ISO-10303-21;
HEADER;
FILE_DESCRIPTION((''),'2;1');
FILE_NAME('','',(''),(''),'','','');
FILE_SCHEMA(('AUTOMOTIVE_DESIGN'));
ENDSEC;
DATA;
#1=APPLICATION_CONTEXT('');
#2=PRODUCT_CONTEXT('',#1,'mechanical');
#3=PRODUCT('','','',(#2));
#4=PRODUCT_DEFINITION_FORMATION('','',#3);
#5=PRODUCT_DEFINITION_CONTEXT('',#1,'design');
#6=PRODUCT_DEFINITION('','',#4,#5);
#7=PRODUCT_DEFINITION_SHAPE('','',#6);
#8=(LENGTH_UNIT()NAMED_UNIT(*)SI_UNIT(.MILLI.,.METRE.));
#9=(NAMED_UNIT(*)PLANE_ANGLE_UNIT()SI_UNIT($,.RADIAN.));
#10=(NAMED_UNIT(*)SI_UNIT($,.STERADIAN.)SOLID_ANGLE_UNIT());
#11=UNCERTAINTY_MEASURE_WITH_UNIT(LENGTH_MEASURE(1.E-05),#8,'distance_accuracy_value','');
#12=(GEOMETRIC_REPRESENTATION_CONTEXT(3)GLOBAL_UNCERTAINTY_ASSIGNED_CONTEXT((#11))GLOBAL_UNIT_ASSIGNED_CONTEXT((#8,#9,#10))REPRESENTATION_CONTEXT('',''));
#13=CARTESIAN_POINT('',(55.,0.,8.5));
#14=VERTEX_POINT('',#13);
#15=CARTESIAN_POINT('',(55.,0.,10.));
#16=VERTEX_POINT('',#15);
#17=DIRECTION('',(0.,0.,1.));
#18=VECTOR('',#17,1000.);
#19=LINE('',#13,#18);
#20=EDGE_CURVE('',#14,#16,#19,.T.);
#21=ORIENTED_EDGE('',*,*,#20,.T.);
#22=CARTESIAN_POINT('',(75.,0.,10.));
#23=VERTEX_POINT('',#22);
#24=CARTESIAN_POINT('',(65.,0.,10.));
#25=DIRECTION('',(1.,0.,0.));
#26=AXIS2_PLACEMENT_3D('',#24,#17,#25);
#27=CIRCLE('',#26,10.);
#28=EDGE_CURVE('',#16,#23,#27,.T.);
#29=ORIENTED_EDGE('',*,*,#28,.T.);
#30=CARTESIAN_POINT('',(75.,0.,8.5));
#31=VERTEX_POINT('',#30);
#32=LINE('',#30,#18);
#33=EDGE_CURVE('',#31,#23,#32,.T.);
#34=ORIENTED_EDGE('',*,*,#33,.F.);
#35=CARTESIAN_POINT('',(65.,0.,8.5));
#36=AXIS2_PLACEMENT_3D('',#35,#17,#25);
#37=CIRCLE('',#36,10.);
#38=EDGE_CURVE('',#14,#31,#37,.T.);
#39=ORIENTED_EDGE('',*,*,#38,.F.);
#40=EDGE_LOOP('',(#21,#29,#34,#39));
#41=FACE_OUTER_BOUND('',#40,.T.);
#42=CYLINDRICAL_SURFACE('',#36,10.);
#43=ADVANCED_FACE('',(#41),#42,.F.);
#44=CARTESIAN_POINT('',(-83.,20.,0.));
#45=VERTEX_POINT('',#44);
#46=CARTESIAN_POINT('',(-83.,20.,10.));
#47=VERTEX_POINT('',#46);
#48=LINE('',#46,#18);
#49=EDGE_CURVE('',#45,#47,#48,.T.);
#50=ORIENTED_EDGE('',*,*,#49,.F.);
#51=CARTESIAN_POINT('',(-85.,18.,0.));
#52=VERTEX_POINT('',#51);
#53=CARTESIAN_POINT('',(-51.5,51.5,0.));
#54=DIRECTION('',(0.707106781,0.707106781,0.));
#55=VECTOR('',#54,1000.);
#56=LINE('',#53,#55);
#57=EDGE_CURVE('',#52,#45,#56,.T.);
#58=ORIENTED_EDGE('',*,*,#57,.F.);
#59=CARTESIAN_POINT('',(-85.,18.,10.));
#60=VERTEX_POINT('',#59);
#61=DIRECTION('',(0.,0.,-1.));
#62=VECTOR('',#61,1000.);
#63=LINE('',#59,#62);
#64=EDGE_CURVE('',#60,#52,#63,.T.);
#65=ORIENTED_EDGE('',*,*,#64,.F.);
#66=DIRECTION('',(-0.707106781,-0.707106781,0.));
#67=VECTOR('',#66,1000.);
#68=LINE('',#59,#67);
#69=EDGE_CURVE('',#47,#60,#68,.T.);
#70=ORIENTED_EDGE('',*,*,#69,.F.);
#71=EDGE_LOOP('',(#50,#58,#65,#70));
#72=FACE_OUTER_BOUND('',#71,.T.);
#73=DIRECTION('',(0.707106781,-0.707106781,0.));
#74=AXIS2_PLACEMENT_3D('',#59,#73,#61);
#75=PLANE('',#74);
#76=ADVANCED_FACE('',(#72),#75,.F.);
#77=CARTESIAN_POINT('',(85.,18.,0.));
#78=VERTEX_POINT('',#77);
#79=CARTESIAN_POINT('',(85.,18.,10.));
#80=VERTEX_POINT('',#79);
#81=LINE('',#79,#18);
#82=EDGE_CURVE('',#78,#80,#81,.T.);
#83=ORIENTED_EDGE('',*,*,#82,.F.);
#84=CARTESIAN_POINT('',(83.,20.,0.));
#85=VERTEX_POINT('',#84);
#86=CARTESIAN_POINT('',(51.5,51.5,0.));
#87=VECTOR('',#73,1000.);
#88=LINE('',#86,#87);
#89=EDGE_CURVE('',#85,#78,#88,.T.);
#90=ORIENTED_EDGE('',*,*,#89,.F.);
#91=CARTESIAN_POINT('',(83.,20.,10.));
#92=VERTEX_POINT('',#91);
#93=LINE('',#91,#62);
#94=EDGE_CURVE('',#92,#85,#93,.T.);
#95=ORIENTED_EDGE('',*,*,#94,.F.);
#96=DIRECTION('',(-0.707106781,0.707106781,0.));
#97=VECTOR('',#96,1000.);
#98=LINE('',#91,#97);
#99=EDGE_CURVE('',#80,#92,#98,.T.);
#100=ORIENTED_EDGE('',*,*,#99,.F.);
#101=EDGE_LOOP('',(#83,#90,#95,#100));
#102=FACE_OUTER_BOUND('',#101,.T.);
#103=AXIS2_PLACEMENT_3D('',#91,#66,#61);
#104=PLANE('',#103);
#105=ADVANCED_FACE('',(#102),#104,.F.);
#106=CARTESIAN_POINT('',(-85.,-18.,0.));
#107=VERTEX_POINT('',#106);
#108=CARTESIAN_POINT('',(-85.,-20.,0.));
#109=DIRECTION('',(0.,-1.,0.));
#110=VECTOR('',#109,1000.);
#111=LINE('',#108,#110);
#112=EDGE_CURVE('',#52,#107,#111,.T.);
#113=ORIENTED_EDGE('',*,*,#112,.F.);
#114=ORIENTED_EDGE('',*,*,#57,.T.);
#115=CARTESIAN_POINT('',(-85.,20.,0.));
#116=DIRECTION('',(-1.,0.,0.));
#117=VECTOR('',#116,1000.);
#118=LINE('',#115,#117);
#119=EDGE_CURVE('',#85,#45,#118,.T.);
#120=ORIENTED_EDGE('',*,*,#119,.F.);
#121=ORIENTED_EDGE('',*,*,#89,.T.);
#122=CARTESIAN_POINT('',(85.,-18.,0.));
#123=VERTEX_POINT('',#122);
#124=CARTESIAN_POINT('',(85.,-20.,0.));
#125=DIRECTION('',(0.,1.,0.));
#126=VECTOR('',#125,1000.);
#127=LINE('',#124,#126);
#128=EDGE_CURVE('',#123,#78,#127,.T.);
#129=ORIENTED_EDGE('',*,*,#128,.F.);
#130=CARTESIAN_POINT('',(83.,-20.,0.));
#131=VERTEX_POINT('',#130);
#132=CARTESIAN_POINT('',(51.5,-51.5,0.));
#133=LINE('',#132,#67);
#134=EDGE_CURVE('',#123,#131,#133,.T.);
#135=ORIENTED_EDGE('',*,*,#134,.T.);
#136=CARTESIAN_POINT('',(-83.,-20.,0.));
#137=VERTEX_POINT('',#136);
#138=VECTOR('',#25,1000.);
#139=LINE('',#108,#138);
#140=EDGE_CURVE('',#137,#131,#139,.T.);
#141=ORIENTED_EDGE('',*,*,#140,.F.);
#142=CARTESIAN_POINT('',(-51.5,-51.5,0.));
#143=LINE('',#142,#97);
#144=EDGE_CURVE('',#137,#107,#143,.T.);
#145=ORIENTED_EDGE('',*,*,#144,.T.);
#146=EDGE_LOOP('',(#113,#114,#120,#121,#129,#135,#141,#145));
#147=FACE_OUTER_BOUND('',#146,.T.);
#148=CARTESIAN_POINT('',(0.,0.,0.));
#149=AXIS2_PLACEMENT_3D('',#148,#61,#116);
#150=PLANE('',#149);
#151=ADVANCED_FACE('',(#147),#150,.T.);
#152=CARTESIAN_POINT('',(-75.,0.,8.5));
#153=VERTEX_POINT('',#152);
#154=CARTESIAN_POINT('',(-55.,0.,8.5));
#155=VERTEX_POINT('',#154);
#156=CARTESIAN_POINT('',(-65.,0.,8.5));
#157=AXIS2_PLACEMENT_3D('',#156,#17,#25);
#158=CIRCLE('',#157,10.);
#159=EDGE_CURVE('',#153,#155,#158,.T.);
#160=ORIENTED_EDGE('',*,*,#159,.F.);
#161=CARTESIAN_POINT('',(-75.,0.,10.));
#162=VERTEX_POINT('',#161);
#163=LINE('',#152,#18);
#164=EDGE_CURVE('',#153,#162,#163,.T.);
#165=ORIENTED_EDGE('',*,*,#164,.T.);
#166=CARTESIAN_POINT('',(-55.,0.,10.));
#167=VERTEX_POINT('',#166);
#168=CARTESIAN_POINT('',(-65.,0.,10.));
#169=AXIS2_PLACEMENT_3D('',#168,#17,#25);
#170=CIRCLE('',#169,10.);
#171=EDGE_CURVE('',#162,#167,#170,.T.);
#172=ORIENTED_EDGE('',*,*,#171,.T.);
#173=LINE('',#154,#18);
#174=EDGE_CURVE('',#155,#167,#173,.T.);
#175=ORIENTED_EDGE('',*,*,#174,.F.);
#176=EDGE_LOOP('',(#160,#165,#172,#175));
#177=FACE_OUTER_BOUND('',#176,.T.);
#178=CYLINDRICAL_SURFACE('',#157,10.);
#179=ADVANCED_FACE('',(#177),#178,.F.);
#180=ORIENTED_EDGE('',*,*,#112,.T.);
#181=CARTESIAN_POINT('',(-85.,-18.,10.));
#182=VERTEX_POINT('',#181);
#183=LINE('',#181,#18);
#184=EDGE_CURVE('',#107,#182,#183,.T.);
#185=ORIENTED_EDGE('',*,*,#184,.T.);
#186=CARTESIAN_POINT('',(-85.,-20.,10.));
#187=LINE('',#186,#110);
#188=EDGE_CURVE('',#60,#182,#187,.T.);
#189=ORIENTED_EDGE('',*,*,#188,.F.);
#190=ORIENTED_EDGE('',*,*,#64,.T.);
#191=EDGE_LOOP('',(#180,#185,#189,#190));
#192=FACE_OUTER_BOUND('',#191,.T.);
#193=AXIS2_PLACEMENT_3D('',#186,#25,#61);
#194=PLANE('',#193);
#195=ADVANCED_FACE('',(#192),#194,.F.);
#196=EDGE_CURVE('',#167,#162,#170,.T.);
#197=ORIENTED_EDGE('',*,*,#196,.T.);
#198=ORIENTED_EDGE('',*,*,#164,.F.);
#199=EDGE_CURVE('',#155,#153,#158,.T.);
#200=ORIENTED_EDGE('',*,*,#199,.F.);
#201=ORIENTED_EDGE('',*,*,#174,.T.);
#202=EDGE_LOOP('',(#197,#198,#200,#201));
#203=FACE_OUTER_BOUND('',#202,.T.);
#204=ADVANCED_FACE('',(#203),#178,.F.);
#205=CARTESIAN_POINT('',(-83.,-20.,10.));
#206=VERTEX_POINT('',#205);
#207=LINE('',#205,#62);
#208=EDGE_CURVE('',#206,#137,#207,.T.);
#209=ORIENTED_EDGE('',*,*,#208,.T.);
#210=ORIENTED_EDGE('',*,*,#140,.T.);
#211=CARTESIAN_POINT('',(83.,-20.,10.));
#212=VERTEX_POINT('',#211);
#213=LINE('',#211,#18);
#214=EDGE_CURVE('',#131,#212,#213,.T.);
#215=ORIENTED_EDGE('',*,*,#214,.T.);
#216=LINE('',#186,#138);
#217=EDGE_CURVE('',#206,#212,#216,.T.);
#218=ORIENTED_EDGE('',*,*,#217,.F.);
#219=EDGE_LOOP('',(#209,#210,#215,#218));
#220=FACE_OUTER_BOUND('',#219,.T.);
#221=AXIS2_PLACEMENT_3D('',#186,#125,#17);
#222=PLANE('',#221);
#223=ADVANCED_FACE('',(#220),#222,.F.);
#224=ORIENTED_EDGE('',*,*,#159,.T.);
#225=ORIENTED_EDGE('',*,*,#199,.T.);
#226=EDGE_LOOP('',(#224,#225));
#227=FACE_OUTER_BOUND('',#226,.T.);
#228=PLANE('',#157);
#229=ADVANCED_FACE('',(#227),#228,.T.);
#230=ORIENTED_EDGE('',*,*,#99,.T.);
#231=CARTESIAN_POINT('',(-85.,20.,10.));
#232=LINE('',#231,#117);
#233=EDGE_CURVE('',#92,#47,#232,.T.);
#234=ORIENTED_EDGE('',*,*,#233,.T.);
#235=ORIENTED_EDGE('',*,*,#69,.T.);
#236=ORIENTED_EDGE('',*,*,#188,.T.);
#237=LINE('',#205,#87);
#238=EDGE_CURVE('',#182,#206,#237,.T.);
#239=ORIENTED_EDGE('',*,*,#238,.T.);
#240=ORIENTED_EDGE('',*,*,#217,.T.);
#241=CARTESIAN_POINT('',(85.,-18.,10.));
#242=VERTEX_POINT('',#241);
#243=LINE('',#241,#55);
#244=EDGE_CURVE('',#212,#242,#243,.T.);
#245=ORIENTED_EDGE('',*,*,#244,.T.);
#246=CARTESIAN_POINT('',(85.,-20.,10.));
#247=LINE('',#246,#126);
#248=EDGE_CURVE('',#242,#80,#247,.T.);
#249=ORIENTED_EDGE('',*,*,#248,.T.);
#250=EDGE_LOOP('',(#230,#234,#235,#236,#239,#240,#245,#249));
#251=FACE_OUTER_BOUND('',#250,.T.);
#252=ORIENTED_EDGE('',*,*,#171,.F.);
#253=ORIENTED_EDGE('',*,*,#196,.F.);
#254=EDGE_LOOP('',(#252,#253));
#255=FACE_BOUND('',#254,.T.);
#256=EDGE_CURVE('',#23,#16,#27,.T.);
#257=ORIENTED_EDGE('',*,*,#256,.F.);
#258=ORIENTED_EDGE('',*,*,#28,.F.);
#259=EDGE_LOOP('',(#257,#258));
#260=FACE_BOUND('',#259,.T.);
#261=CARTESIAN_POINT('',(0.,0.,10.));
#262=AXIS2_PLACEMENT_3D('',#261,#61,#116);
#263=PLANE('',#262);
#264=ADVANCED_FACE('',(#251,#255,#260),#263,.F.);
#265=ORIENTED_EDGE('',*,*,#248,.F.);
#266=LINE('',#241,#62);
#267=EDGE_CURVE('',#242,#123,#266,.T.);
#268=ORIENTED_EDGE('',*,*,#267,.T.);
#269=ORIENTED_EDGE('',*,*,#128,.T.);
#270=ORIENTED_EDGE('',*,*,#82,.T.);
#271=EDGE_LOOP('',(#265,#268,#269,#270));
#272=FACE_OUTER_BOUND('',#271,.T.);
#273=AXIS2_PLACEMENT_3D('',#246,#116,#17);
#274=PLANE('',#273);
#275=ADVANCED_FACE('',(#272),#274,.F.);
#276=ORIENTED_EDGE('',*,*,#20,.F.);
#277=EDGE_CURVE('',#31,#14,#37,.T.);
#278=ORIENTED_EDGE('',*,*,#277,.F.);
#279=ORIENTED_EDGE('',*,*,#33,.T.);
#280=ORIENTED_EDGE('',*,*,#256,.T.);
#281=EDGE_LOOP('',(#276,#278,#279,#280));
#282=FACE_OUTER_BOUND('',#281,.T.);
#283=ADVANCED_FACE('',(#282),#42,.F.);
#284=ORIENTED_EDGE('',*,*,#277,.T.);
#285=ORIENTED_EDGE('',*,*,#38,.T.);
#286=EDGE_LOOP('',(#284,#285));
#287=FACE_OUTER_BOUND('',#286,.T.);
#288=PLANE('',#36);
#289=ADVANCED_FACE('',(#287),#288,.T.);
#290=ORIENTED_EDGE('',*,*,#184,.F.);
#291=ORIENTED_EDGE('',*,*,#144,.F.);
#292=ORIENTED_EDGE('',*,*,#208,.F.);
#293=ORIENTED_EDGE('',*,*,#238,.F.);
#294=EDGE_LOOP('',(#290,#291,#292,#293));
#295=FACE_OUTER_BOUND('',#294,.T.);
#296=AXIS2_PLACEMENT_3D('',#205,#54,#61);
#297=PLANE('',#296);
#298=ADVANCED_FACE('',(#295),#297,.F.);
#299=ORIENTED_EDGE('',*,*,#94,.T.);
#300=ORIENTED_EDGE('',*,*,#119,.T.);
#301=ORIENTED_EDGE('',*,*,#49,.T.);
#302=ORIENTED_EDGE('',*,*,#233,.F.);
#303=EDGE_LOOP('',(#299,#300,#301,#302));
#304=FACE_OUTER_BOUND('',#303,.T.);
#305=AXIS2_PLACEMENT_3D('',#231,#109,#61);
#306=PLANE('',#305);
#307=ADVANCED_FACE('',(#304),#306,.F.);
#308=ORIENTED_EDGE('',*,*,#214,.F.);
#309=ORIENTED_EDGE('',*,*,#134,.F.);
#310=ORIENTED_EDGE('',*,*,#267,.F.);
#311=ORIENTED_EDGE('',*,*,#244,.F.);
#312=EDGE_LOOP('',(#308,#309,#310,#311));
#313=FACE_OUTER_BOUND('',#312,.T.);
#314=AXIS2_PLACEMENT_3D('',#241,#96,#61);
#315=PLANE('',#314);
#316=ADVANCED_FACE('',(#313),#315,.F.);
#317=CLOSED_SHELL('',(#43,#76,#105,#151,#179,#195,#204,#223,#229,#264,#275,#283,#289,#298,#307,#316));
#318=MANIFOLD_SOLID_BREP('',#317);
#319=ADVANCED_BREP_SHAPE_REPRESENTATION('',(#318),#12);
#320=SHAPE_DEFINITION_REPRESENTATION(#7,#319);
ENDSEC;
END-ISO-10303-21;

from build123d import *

# Parameters (mm, degrees)
SKETCH_1_W          = 170
SKETCH_1_H          = 40
EXTRUDE_1_DEPTH     = 10
SKETCH_2_R          = 10
CUT_EXTRUDE_1_DEPTH = 1.5
CHAMFER_1_SIZE      = 2


with BuildPart() as part:
    # 草图1 → 凸台-拉伸1 (new body)
    with BuildSketch(Plane.XY):
        Rectangle(SKETCH_1_W, SKETCH_1_H)
    extrude(amount=EXTRUDE_1_DEPTH)

    # 草图2 → 切除-拉伸1 (cut)
    with BuildSketch(Plane.XY.offset(10)):
        with Locations((-65, 0)):
            Circle(SKETCH_2_R)
        with Locations((65, 0)):
            Circle(SKETCH_2_R)
    extrude(amount=-CUT_EXTRUDE_1_DEPTH, mode=Mode.SUBTRACT)

    # 倒角1
    chamfer_1_edges = [part.edges().sort_by_distance(p)[0] for p in [
        (85, -20, 5),
        (-85, -20, 5),
        (-85, 20, 5),
        (85, 20, 5),
    ]]
    chamfer(chamfer_1_edges, length=CHAMFER_1_SIZE)


solid = part.part
